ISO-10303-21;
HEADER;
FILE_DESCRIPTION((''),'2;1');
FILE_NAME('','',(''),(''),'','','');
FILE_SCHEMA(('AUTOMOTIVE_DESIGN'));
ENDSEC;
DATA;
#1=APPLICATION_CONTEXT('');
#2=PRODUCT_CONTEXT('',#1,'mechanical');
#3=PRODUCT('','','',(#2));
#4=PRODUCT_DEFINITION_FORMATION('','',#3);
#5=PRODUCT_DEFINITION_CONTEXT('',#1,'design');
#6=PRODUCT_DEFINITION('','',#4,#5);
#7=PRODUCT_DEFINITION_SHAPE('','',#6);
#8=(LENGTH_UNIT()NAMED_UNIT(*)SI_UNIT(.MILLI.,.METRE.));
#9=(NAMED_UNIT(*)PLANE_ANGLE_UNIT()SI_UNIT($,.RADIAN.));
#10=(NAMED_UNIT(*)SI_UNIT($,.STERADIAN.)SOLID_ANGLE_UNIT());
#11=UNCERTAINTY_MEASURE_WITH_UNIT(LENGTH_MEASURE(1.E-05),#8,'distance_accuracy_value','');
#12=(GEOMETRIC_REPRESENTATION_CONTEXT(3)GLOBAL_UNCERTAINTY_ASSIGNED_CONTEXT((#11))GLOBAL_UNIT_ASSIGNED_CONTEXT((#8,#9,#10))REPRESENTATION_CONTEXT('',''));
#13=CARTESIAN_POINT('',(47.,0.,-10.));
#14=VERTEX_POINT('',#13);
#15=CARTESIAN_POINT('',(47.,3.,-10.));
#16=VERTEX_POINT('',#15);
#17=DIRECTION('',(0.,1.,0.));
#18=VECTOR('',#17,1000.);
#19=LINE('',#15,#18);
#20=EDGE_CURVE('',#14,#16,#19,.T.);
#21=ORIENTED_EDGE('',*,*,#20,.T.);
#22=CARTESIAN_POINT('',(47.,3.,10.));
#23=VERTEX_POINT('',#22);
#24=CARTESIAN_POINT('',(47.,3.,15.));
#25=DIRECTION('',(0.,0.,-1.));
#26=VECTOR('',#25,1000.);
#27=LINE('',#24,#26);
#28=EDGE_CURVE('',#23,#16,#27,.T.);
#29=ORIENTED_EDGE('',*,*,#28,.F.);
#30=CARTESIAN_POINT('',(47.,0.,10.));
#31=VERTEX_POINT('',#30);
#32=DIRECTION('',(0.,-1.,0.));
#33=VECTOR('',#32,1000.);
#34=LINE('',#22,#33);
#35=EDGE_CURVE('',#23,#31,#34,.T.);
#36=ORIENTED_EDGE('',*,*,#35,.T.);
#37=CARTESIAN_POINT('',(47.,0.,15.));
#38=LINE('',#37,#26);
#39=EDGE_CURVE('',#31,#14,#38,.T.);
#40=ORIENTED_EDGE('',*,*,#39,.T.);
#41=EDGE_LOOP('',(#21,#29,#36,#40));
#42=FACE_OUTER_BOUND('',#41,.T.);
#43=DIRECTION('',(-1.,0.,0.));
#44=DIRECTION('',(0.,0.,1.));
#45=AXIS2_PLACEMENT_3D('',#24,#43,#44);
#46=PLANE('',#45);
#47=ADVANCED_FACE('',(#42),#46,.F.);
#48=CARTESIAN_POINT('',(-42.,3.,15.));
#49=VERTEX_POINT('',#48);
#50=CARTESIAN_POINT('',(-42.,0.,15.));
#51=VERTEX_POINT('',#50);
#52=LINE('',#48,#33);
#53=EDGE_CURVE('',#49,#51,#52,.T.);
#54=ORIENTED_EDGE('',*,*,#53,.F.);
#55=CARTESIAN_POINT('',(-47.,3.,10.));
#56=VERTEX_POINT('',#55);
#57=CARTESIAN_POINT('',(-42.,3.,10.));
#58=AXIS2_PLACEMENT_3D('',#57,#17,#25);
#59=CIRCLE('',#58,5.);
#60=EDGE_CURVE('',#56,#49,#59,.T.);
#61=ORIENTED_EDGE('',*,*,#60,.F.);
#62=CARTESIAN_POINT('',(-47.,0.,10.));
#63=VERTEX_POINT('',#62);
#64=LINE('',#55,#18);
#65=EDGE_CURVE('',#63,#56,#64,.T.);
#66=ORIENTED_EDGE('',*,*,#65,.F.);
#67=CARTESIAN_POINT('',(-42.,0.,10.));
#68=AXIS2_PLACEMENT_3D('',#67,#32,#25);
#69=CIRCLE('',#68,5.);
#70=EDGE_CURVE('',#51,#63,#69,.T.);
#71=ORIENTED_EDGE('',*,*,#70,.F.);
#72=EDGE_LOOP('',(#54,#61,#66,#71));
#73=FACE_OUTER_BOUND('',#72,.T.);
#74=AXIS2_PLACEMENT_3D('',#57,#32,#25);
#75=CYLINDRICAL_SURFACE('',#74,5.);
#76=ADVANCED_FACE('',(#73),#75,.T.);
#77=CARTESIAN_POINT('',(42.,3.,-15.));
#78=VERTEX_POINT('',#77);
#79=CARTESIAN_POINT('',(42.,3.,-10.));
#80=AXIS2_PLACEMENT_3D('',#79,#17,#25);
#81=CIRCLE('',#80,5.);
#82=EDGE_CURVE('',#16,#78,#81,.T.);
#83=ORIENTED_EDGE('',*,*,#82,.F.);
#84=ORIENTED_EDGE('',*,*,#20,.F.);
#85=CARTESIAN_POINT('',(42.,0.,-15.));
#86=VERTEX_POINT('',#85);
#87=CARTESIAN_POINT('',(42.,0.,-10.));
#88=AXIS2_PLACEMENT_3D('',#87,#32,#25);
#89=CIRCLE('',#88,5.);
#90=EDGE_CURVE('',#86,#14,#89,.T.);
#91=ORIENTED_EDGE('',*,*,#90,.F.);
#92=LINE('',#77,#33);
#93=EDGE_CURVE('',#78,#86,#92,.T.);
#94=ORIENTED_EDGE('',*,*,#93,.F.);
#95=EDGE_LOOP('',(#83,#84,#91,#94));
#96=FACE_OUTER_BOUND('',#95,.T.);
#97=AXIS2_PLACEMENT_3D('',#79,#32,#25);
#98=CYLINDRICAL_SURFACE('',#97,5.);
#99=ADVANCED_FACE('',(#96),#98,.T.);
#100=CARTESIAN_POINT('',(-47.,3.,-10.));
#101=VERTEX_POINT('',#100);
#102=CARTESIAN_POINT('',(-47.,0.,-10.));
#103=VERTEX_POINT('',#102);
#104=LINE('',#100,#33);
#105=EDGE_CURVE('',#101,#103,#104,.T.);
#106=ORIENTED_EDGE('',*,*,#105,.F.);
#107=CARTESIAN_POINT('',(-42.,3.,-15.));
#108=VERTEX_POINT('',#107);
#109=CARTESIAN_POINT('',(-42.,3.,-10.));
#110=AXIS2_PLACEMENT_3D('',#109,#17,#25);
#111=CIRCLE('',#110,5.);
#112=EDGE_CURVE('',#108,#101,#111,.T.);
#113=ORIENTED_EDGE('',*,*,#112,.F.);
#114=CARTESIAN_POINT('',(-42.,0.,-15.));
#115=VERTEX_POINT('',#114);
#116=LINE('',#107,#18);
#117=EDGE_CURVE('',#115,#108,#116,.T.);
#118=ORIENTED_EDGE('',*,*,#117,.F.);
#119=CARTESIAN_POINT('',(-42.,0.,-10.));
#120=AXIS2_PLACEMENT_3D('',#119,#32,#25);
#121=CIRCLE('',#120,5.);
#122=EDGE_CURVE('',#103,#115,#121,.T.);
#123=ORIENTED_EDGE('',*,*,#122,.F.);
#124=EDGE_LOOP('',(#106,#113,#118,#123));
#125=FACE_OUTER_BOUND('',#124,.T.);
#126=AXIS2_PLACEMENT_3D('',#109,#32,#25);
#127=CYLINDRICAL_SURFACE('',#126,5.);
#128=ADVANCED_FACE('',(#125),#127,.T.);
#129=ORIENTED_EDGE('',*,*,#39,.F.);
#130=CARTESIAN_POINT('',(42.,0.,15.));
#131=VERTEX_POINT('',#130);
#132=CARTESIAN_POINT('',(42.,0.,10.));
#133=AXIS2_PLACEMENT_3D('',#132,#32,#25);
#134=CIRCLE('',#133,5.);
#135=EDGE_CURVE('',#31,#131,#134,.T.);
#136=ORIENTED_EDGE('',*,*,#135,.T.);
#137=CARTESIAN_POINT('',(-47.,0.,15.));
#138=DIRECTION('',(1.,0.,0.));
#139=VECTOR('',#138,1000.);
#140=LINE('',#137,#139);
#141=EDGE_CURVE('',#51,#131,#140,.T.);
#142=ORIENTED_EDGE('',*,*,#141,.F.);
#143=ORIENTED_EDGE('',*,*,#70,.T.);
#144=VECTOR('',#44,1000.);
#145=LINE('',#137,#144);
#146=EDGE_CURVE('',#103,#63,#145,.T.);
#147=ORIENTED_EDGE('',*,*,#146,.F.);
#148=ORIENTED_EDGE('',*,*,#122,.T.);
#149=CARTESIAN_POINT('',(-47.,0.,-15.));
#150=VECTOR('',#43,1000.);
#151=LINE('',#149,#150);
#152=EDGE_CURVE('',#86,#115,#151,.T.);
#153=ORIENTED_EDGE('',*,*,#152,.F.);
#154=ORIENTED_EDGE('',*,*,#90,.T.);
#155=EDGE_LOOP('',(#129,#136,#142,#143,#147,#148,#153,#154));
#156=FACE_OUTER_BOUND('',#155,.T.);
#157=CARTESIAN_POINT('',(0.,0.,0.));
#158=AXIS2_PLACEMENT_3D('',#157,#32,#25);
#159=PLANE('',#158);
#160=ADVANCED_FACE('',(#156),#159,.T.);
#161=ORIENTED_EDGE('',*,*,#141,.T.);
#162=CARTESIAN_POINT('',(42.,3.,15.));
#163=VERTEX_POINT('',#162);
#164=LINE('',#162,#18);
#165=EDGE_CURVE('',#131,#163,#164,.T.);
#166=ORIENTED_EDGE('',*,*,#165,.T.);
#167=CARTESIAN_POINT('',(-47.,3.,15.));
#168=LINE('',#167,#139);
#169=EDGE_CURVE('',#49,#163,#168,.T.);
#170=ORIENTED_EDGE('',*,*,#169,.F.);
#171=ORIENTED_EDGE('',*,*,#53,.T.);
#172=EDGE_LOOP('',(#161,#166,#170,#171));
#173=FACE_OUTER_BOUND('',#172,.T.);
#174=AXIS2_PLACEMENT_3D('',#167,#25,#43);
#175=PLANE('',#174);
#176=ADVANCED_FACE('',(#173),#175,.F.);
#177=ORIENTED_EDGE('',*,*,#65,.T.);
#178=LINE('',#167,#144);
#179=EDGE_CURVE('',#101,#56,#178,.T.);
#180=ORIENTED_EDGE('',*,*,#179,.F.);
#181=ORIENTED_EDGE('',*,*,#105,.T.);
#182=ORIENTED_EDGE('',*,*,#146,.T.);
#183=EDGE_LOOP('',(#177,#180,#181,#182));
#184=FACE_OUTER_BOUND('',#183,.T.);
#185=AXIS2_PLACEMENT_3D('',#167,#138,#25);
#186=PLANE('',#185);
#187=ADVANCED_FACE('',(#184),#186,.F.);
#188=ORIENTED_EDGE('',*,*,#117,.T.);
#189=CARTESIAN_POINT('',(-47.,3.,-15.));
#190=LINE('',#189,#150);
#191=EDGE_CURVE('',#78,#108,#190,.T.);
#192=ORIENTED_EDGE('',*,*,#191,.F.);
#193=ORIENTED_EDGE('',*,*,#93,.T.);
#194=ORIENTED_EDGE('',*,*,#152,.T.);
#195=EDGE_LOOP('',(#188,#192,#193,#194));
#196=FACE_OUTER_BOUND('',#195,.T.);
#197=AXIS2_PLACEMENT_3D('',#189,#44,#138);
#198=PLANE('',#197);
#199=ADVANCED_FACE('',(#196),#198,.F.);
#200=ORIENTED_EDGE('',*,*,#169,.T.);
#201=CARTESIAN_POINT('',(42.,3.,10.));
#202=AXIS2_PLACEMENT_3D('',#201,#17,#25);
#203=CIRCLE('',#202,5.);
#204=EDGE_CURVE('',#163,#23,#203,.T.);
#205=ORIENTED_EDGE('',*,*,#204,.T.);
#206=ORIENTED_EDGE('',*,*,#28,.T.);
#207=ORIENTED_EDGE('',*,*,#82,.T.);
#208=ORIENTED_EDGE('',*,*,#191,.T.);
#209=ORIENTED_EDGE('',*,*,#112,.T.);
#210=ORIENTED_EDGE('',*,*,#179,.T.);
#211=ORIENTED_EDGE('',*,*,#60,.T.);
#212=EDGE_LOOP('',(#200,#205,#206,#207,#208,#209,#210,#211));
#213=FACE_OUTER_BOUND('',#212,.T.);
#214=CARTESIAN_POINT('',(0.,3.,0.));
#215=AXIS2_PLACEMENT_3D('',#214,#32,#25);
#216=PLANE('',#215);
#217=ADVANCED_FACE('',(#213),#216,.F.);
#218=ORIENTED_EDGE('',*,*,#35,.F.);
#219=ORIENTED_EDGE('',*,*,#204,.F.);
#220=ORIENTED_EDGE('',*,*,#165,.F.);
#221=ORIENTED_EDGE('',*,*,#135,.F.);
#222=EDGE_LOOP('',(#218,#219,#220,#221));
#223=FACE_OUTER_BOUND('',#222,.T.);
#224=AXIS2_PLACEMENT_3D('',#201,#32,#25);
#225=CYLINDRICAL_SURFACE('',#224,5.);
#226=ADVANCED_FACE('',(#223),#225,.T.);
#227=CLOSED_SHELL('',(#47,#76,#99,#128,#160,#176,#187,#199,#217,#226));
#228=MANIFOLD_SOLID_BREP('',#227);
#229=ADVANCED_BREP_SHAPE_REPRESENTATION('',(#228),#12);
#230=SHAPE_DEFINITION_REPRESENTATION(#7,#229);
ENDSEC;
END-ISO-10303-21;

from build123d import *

# Parameters (mm, degrees)
SKETCH1_W           = 94
SKETCH1_H           = 30
BOSS_EXTRUDE1_DEPTH = 3
FILLET1_R           = 5


with BuildPart() as part:
    # Sketch1 → Boss-Extrude1 (new body)
    with BuildSketch(Plane(origin=(0, 0, 0), x_dir=(1, 0, 0), z_dir=(0, 1, 0))):
        Rectangle(SKETCH1_W, SKETCH1_H)
    extrude(amount=BOSS_EXTRUDE1_DEPTH)

    # Fillet1
    fillet1_edges = [part.edges().sort_by_distance(p)[0] for p in [
        (47, 1.5, 15),
        (-47, 1.5, 15),
        (-47, 1.5, -15),
        (47, 1.5, -15),
    ]]
    fillet(fillet1_edges, radius=FILLET1_R)


solid = part.part
